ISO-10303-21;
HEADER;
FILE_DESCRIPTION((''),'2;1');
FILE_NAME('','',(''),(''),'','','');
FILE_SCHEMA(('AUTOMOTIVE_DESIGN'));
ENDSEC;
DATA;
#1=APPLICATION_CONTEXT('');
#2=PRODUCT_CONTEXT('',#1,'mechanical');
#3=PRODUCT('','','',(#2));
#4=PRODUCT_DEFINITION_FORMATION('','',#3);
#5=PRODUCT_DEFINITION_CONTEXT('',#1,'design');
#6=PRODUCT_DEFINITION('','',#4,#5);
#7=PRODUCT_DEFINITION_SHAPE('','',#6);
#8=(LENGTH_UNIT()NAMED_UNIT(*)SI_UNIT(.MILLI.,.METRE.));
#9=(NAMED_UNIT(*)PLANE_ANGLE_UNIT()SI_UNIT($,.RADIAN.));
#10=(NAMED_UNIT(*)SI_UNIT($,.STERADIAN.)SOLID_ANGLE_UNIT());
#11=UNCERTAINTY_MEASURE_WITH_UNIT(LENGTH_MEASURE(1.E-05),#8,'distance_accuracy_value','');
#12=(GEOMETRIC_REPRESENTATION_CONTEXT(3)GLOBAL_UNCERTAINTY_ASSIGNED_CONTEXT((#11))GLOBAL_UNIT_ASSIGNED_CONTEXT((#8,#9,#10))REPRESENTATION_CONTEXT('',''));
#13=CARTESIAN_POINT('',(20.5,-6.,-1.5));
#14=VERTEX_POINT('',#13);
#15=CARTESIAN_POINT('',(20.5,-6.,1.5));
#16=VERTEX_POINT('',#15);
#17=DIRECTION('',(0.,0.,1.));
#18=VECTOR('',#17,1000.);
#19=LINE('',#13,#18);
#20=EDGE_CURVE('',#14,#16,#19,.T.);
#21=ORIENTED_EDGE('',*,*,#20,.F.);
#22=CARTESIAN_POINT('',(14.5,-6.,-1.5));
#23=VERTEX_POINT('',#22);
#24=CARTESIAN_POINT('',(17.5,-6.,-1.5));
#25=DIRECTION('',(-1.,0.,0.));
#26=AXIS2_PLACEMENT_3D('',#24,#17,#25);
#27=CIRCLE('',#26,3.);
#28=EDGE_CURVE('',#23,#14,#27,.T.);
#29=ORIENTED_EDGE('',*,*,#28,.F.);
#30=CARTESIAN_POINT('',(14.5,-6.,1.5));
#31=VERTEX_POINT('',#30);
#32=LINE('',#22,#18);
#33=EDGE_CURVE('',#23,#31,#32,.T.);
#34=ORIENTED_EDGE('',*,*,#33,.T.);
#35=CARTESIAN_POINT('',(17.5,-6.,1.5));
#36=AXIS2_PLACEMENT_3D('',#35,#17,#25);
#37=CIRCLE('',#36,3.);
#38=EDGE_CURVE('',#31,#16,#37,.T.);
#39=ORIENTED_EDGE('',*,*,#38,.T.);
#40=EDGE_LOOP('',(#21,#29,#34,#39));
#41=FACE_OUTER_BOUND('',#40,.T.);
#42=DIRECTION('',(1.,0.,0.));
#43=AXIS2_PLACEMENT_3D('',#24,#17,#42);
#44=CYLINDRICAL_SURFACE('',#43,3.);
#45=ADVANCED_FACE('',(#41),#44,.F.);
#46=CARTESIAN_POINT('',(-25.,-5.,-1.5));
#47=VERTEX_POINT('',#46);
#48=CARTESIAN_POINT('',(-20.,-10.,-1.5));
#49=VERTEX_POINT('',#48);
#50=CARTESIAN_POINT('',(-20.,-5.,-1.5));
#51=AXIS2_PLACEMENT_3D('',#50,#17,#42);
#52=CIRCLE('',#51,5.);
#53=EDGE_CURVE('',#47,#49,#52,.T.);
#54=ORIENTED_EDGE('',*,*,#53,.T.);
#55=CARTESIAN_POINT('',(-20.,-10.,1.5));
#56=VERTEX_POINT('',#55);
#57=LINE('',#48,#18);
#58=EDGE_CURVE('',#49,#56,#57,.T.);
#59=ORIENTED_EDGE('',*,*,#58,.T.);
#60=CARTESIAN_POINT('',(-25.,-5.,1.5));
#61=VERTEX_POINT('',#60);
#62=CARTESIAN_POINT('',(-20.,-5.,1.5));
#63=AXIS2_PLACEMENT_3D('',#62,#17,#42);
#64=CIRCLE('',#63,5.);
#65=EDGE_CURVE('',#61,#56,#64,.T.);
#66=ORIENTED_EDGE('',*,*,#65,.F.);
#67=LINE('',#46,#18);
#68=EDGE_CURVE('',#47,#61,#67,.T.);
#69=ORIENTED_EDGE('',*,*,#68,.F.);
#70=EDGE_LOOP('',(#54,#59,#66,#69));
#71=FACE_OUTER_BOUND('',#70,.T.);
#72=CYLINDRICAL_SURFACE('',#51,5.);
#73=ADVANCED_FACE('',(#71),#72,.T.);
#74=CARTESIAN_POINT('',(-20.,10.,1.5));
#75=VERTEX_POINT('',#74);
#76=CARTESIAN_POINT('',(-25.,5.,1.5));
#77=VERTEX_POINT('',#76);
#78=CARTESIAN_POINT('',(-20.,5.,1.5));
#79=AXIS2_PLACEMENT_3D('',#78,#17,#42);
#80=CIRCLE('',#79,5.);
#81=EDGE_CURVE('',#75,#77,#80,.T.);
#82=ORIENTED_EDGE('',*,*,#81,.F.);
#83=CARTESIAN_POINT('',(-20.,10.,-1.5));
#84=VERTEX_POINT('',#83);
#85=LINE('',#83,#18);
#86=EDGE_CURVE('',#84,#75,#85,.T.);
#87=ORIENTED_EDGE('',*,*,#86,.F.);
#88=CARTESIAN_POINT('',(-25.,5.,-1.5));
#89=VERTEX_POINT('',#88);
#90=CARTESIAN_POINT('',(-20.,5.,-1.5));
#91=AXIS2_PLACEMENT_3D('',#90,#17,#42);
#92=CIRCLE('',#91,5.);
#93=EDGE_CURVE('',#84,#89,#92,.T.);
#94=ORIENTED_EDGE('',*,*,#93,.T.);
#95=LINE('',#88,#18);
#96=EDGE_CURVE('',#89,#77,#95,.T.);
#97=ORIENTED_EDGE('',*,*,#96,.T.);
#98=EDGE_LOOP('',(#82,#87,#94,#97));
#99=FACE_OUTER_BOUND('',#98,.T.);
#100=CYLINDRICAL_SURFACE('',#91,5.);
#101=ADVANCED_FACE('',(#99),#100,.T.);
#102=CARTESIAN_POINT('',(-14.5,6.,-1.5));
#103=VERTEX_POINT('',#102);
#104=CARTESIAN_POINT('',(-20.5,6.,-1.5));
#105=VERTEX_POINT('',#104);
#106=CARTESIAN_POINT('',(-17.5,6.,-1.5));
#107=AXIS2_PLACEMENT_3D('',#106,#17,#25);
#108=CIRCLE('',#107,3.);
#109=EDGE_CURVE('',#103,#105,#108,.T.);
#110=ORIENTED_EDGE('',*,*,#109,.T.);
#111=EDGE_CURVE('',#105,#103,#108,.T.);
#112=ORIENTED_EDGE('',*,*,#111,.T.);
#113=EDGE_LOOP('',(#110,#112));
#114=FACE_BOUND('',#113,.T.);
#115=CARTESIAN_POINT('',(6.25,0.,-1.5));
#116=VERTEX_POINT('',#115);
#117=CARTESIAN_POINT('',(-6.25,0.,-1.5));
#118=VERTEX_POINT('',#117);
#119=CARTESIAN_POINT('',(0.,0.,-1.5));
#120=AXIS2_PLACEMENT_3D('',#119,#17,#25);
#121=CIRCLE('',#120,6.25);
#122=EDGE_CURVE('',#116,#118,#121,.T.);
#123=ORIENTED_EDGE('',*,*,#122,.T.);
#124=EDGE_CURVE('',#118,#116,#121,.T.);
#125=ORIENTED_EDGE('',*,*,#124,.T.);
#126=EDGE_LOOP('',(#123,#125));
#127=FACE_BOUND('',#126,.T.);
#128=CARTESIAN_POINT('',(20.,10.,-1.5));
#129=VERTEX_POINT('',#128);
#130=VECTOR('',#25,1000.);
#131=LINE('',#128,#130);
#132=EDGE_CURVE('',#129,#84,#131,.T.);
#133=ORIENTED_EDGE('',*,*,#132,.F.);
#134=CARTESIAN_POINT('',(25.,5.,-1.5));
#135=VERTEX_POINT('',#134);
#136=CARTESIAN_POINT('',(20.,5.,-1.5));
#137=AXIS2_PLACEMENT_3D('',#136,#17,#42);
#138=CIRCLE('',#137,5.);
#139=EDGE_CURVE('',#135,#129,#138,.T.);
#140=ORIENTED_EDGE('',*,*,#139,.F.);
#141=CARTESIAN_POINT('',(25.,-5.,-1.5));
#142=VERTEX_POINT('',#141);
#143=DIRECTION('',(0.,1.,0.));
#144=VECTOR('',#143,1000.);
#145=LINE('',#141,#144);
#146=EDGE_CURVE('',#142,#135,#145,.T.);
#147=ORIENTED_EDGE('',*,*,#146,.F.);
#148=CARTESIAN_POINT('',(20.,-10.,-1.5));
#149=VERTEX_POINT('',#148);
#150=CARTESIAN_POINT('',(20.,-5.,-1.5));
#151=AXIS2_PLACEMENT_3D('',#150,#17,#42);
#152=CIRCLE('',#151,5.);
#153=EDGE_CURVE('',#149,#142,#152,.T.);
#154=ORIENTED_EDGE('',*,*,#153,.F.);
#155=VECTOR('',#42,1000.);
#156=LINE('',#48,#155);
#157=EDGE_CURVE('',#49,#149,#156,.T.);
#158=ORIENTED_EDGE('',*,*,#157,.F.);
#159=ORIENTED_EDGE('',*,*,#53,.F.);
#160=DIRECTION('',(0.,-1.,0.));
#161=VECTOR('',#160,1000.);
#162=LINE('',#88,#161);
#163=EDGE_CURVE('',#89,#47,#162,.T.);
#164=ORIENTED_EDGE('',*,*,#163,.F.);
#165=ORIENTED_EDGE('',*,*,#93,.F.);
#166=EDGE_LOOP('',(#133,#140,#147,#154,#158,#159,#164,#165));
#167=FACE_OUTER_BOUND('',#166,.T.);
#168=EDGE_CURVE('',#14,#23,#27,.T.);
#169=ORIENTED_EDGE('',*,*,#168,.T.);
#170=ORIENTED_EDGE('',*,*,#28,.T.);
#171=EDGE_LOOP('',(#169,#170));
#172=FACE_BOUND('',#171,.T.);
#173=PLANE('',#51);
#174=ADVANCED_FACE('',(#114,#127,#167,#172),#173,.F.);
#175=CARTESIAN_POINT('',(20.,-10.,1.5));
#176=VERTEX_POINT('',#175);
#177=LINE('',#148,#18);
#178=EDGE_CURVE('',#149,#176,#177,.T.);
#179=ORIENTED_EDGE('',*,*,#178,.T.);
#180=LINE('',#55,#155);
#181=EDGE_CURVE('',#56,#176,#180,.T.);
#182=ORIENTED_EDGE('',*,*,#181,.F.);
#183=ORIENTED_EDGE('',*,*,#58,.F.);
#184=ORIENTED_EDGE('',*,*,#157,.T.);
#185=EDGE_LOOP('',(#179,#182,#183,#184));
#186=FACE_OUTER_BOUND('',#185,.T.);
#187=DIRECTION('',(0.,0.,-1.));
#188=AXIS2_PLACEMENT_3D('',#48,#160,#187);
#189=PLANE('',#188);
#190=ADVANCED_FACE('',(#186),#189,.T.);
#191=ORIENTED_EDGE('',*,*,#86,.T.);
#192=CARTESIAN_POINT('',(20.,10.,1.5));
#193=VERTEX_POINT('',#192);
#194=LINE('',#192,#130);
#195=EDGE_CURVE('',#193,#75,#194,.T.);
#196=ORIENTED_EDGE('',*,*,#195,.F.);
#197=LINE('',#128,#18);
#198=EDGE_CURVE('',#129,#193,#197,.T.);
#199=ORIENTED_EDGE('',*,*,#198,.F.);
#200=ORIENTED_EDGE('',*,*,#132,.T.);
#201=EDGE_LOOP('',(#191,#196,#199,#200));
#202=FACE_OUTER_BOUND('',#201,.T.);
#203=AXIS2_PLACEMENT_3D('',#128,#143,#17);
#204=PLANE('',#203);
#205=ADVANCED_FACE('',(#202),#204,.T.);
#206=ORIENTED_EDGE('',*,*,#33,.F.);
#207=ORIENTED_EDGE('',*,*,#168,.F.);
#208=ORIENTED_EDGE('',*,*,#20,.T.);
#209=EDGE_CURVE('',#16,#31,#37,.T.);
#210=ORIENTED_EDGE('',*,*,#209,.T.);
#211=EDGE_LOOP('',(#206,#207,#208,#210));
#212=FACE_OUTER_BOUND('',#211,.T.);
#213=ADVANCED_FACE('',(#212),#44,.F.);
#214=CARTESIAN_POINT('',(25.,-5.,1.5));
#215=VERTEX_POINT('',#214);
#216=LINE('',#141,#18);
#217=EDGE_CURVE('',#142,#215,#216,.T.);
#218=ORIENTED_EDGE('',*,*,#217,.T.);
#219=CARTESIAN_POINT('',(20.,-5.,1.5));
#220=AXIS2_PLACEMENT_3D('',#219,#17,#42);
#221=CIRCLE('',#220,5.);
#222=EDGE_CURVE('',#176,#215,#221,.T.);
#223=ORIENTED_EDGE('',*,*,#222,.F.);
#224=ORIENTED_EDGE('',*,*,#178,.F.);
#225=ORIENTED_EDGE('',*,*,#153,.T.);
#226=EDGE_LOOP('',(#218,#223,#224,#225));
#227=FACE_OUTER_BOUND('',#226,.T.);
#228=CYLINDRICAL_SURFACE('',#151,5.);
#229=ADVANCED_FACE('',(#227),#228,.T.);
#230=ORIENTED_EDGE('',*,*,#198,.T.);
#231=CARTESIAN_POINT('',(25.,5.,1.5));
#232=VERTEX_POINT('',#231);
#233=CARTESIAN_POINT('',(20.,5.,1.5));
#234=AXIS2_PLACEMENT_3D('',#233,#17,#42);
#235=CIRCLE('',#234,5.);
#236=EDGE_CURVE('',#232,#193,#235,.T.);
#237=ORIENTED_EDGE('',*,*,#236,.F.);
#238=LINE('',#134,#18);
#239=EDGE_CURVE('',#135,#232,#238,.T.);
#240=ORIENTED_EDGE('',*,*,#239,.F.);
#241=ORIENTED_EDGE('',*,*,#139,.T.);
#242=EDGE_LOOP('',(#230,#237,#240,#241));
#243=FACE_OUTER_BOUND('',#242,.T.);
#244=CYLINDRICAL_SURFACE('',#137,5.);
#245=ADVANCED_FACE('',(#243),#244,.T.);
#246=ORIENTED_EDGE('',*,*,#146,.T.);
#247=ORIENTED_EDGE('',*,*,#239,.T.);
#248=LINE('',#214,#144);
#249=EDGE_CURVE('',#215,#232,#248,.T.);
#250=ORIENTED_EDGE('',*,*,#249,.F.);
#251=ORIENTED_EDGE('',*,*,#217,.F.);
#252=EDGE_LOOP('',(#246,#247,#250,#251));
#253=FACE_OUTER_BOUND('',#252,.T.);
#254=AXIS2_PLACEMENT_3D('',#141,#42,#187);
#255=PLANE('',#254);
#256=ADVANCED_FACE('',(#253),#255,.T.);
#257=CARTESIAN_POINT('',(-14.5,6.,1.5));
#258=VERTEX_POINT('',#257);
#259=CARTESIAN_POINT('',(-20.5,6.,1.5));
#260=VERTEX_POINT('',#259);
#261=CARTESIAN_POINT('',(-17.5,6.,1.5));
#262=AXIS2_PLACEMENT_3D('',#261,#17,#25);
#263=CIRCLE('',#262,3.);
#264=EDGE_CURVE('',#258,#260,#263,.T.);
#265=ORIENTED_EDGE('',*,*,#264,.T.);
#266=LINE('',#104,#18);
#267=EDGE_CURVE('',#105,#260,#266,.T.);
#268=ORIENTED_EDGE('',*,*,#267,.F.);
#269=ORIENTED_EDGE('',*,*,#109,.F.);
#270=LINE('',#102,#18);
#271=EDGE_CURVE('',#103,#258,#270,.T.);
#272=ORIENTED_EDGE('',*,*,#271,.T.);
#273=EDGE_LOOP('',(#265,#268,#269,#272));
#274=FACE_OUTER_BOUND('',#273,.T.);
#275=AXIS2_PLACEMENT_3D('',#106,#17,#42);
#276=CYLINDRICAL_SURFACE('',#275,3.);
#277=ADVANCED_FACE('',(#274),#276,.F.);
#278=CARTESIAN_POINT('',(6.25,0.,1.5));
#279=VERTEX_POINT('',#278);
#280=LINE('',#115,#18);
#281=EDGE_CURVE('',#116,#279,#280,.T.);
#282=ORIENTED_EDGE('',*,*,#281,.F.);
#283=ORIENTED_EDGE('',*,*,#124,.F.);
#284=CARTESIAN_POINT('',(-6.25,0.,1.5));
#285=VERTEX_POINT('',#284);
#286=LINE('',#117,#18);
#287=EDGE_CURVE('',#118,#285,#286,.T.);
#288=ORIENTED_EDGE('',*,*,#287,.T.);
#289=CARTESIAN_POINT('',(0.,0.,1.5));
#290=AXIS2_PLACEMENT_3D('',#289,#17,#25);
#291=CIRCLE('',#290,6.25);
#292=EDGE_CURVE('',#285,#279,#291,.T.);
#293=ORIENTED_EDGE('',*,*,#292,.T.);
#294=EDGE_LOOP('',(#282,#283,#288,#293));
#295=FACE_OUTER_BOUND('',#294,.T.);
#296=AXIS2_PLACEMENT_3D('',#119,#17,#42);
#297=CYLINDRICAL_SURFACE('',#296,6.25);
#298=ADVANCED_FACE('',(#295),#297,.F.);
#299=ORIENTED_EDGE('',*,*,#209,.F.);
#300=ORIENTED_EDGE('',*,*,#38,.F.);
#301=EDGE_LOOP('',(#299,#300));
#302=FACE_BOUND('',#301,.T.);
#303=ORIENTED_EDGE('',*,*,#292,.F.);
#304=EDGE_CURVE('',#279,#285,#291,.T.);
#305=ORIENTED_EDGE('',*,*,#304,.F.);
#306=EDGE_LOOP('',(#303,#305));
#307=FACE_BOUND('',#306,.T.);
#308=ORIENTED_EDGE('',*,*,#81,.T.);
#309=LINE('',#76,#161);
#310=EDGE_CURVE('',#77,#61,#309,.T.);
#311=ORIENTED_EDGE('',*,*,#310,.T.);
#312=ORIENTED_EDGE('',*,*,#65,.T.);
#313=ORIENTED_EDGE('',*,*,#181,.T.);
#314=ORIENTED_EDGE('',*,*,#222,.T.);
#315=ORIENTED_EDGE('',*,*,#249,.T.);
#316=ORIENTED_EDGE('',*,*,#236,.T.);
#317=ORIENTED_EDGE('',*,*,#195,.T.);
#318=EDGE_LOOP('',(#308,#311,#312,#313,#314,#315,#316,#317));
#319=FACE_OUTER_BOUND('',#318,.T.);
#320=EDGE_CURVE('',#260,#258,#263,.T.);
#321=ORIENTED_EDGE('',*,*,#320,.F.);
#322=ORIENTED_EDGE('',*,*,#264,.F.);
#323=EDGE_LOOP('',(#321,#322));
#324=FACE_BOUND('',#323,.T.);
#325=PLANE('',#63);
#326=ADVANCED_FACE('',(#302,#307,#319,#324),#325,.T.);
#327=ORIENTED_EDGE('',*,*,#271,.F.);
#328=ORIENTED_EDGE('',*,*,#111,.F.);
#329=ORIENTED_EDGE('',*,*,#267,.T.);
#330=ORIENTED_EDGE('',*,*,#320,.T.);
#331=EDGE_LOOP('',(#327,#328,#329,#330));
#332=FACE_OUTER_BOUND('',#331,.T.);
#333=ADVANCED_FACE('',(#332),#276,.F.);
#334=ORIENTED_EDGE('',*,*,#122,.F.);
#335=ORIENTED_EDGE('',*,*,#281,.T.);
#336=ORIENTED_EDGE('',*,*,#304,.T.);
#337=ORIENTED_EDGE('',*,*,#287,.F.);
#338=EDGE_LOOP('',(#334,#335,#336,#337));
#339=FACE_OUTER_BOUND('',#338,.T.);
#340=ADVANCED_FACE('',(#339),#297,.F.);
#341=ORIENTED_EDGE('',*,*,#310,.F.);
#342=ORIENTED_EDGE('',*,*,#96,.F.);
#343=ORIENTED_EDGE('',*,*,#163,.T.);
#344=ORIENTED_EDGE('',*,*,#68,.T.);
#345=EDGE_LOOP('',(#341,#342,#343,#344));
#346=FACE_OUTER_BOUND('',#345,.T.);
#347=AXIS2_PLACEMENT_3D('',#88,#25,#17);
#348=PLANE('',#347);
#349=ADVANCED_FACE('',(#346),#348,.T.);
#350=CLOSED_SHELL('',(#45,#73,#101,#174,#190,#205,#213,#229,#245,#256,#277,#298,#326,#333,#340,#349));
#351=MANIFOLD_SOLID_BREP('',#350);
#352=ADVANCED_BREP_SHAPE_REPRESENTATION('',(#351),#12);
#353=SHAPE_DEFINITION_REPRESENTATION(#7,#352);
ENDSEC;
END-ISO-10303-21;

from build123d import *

# Parameters (mm, degrees)
SKETCH_1_R      = 3
SKETCH_1_R_2    = 6.25
EXTRUDE_1_DEPTH = 3


with BuildPart() as part:
    # 草图1 → 凸台-拉伸1 (new body)
    with BuildSketch(Plane.XY.offset(1.5)):
        with BuildLine():
            Line((-20, -10), (20, -10))
            ThreePointArc((20, -10), (23.535533906, -8.535533906), (25, -5))
            Line((25, -5), (25, 5))
            ThreePointArc((25, 5), (23.535533906, 8.535533906), (20, 10))
            Line((20, 10), (-20, 10))
            ThreePointArc((-20, 10), (-23.535533906, 8.535533906), (-25, 5))
            Line((-25, 5), (-25, -5))
            ThreePointArc((-25, -5), (-23.535533906, -8.535533906), (-20, -10))
        make_face()
        with Locations(Location((-17.5, 6, 0), (0, 0, 180))):
            Circle(SKETCH_1_R, mode=Mode.SUBTRACT)
        with Locations(Location((17.5, -6, 0), (0, 0, 180))):
            Circle(SKETCH_1_R, mode=Mode.SUBTRACT)
        with Locations(Location((0, 0, 0), (0, 0, 180))):
            Circle(SKETCH_1_R_2, mode=Mode.SUBTRACT)
    extrude(amount=-EXTRUDE_1_DEPTH)


solid = part.part
